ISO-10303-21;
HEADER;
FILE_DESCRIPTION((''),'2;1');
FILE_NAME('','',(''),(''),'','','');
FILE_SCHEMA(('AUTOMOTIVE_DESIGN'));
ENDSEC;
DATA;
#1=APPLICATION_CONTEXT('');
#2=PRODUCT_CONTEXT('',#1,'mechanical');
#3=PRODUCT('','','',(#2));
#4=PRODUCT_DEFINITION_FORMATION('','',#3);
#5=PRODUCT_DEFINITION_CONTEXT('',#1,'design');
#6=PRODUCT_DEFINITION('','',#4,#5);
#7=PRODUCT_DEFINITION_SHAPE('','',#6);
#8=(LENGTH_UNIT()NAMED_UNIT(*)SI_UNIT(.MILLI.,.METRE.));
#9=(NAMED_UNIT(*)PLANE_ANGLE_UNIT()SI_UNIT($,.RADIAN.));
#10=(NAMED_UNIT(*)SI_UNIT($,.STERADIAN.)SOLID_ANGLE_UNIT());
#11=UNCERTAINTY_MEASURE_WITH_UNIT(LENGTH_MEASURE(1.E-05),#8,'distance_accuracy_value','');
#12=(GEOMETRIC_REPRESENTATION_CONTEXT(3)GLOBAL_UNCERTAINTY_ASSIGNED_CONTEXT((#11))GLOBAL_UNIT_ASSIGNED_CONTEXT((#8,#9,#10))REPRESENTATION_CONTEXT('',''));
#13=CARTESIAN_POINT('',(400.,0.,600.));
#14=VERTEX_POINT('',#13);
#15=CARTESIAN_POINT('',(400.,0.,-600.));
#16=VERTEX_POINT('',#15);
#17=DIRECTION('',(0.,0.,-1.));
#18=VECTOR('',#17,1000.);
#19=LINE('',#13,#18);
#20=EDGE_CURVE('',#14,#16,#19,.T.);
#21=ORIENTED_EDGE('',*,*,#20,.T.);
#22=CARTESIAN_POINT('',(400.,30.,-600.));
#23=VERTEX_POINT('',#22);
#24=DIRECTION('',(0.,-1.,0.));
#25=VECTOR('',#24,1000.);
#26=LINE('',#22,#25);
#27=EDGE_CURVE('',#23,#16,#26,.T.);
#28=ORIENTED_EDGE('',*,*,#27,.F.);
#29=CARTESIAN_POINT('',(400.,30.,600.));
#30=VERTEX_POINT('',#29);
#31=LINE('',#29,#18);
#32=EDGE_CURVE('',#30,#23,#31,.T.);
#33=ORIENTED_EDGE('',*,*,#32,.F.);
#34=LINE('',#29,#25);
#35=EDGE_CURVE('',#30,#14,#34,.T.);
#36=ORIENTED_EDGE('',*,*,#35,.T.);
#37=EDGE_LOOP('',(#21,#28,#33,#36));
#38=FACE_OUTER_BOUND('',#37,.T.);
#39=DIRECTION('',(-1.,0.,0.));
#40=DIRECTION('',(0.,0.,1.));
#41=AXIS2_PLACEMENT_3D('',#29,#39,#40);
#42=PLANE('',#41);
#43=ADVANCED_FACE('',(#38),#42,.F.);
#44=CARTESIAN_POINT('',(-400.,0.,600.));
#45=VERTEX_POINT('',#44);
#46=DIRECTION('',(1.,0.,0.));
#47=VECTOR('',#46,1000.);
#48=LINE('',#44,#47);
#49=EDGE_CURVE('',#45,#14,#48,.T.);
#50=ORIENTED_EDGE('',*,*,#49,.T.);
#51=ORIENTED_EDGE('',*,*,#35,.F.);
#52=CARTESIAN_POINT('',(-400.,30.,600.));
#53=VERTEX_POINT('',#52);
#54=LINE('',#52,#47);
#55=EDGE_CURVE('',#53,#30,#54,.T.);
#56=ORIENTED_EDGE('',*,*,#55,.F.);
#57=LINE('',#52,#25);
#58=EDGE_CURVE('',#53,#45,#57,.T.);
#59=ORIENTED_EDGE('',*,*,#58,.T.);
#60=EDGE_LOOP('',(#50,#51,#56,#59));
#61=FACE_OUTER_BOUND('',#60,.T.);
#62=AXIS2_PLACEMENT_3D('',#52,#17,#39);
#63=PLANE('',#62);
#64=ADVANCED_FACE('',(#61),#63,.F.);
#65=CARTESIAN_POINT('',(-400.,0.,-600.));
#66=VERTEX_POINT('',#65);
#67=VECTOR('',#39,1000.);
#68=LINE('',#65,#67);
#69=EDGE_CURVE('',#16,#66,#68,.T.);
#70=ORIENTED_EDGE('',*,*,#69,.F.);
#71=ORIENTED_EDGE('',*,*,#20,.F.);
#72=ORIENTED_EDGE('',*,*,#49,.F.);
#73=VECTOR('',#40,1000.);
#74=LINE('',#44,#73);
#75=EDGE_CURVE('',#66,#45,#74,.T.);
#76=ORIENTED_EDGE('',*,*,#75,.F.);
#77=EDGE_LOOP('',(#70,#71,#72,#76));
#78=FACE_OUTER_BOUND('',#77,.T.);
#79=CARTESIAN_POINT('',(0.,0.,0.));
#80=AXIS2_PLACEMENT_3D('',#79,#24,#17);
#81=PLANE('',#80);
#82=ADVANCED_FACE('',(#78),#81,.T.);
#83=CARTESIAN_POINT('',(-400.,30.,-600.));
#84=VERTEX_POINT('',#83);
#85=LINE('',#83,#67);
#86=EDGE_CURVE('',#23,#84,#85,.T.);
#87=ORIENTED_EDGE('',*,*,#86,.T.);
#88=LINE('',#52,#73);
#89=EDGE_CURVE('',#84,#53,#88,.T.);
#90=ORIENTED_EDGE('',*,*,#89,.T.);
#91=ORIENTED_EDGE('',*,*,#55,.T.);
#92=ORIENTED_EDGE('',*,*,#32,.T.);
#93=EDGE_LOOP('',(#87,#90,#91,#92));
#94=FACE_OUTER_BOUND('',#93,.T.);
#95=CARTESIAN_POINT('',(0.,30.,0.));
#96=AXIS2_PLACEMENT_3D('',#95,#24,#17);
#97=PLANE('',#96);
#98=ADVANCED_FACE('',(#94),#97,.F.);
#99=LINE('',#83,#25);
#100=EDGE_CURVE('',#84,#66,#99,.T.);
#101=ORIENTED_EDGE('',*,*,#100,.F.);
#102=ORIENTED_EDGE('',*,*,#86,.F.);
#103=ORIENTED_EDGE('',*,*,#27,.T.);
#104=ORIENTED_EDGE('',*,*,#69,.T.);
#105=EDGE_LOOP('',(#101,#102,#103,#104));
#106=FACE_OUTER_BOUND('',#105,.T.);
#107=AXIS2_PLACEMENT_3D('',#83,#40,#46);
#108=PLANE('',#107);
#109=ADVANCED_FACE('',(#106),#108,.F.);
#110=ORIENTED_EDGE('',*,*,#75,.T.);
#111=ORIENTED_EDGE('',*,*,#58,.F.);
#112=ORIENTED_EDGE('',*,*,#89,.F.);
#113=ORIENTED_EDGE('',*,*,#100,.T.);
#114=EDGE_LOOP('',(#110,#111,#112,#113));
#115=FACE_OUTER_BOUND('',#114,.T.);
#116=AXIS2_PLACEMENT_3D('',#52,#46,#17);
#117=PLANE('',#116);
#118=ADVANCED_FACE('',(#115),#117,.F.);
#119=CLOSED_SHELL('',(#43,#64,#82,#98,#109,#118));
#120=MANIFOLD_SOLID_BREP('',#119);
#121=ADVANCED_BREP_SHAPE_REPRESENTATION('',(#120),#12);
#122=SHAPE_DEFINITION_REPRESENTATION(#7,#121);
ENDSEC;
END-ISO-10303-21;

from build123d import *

# Parameters (mm, degrees)
SKETCH_1_W      = 800
SKETCH_1_H      = 1200
EXTRUDE_1_DEPTH = 30


with BuildPart() as part:
    # 草图1 → 凸台-拉伸1 (new body)
    with BuildSketch(Plane(origin=(0, 0, 0), x_dir=(1, 0, 0), z_dir=(0, 1, 0))):
        Rectangle(SKETCH_1_W, SKETCH_1_H)
    extrude(amount=EXTRUDE_1_DEPTH)


solid = part.part
